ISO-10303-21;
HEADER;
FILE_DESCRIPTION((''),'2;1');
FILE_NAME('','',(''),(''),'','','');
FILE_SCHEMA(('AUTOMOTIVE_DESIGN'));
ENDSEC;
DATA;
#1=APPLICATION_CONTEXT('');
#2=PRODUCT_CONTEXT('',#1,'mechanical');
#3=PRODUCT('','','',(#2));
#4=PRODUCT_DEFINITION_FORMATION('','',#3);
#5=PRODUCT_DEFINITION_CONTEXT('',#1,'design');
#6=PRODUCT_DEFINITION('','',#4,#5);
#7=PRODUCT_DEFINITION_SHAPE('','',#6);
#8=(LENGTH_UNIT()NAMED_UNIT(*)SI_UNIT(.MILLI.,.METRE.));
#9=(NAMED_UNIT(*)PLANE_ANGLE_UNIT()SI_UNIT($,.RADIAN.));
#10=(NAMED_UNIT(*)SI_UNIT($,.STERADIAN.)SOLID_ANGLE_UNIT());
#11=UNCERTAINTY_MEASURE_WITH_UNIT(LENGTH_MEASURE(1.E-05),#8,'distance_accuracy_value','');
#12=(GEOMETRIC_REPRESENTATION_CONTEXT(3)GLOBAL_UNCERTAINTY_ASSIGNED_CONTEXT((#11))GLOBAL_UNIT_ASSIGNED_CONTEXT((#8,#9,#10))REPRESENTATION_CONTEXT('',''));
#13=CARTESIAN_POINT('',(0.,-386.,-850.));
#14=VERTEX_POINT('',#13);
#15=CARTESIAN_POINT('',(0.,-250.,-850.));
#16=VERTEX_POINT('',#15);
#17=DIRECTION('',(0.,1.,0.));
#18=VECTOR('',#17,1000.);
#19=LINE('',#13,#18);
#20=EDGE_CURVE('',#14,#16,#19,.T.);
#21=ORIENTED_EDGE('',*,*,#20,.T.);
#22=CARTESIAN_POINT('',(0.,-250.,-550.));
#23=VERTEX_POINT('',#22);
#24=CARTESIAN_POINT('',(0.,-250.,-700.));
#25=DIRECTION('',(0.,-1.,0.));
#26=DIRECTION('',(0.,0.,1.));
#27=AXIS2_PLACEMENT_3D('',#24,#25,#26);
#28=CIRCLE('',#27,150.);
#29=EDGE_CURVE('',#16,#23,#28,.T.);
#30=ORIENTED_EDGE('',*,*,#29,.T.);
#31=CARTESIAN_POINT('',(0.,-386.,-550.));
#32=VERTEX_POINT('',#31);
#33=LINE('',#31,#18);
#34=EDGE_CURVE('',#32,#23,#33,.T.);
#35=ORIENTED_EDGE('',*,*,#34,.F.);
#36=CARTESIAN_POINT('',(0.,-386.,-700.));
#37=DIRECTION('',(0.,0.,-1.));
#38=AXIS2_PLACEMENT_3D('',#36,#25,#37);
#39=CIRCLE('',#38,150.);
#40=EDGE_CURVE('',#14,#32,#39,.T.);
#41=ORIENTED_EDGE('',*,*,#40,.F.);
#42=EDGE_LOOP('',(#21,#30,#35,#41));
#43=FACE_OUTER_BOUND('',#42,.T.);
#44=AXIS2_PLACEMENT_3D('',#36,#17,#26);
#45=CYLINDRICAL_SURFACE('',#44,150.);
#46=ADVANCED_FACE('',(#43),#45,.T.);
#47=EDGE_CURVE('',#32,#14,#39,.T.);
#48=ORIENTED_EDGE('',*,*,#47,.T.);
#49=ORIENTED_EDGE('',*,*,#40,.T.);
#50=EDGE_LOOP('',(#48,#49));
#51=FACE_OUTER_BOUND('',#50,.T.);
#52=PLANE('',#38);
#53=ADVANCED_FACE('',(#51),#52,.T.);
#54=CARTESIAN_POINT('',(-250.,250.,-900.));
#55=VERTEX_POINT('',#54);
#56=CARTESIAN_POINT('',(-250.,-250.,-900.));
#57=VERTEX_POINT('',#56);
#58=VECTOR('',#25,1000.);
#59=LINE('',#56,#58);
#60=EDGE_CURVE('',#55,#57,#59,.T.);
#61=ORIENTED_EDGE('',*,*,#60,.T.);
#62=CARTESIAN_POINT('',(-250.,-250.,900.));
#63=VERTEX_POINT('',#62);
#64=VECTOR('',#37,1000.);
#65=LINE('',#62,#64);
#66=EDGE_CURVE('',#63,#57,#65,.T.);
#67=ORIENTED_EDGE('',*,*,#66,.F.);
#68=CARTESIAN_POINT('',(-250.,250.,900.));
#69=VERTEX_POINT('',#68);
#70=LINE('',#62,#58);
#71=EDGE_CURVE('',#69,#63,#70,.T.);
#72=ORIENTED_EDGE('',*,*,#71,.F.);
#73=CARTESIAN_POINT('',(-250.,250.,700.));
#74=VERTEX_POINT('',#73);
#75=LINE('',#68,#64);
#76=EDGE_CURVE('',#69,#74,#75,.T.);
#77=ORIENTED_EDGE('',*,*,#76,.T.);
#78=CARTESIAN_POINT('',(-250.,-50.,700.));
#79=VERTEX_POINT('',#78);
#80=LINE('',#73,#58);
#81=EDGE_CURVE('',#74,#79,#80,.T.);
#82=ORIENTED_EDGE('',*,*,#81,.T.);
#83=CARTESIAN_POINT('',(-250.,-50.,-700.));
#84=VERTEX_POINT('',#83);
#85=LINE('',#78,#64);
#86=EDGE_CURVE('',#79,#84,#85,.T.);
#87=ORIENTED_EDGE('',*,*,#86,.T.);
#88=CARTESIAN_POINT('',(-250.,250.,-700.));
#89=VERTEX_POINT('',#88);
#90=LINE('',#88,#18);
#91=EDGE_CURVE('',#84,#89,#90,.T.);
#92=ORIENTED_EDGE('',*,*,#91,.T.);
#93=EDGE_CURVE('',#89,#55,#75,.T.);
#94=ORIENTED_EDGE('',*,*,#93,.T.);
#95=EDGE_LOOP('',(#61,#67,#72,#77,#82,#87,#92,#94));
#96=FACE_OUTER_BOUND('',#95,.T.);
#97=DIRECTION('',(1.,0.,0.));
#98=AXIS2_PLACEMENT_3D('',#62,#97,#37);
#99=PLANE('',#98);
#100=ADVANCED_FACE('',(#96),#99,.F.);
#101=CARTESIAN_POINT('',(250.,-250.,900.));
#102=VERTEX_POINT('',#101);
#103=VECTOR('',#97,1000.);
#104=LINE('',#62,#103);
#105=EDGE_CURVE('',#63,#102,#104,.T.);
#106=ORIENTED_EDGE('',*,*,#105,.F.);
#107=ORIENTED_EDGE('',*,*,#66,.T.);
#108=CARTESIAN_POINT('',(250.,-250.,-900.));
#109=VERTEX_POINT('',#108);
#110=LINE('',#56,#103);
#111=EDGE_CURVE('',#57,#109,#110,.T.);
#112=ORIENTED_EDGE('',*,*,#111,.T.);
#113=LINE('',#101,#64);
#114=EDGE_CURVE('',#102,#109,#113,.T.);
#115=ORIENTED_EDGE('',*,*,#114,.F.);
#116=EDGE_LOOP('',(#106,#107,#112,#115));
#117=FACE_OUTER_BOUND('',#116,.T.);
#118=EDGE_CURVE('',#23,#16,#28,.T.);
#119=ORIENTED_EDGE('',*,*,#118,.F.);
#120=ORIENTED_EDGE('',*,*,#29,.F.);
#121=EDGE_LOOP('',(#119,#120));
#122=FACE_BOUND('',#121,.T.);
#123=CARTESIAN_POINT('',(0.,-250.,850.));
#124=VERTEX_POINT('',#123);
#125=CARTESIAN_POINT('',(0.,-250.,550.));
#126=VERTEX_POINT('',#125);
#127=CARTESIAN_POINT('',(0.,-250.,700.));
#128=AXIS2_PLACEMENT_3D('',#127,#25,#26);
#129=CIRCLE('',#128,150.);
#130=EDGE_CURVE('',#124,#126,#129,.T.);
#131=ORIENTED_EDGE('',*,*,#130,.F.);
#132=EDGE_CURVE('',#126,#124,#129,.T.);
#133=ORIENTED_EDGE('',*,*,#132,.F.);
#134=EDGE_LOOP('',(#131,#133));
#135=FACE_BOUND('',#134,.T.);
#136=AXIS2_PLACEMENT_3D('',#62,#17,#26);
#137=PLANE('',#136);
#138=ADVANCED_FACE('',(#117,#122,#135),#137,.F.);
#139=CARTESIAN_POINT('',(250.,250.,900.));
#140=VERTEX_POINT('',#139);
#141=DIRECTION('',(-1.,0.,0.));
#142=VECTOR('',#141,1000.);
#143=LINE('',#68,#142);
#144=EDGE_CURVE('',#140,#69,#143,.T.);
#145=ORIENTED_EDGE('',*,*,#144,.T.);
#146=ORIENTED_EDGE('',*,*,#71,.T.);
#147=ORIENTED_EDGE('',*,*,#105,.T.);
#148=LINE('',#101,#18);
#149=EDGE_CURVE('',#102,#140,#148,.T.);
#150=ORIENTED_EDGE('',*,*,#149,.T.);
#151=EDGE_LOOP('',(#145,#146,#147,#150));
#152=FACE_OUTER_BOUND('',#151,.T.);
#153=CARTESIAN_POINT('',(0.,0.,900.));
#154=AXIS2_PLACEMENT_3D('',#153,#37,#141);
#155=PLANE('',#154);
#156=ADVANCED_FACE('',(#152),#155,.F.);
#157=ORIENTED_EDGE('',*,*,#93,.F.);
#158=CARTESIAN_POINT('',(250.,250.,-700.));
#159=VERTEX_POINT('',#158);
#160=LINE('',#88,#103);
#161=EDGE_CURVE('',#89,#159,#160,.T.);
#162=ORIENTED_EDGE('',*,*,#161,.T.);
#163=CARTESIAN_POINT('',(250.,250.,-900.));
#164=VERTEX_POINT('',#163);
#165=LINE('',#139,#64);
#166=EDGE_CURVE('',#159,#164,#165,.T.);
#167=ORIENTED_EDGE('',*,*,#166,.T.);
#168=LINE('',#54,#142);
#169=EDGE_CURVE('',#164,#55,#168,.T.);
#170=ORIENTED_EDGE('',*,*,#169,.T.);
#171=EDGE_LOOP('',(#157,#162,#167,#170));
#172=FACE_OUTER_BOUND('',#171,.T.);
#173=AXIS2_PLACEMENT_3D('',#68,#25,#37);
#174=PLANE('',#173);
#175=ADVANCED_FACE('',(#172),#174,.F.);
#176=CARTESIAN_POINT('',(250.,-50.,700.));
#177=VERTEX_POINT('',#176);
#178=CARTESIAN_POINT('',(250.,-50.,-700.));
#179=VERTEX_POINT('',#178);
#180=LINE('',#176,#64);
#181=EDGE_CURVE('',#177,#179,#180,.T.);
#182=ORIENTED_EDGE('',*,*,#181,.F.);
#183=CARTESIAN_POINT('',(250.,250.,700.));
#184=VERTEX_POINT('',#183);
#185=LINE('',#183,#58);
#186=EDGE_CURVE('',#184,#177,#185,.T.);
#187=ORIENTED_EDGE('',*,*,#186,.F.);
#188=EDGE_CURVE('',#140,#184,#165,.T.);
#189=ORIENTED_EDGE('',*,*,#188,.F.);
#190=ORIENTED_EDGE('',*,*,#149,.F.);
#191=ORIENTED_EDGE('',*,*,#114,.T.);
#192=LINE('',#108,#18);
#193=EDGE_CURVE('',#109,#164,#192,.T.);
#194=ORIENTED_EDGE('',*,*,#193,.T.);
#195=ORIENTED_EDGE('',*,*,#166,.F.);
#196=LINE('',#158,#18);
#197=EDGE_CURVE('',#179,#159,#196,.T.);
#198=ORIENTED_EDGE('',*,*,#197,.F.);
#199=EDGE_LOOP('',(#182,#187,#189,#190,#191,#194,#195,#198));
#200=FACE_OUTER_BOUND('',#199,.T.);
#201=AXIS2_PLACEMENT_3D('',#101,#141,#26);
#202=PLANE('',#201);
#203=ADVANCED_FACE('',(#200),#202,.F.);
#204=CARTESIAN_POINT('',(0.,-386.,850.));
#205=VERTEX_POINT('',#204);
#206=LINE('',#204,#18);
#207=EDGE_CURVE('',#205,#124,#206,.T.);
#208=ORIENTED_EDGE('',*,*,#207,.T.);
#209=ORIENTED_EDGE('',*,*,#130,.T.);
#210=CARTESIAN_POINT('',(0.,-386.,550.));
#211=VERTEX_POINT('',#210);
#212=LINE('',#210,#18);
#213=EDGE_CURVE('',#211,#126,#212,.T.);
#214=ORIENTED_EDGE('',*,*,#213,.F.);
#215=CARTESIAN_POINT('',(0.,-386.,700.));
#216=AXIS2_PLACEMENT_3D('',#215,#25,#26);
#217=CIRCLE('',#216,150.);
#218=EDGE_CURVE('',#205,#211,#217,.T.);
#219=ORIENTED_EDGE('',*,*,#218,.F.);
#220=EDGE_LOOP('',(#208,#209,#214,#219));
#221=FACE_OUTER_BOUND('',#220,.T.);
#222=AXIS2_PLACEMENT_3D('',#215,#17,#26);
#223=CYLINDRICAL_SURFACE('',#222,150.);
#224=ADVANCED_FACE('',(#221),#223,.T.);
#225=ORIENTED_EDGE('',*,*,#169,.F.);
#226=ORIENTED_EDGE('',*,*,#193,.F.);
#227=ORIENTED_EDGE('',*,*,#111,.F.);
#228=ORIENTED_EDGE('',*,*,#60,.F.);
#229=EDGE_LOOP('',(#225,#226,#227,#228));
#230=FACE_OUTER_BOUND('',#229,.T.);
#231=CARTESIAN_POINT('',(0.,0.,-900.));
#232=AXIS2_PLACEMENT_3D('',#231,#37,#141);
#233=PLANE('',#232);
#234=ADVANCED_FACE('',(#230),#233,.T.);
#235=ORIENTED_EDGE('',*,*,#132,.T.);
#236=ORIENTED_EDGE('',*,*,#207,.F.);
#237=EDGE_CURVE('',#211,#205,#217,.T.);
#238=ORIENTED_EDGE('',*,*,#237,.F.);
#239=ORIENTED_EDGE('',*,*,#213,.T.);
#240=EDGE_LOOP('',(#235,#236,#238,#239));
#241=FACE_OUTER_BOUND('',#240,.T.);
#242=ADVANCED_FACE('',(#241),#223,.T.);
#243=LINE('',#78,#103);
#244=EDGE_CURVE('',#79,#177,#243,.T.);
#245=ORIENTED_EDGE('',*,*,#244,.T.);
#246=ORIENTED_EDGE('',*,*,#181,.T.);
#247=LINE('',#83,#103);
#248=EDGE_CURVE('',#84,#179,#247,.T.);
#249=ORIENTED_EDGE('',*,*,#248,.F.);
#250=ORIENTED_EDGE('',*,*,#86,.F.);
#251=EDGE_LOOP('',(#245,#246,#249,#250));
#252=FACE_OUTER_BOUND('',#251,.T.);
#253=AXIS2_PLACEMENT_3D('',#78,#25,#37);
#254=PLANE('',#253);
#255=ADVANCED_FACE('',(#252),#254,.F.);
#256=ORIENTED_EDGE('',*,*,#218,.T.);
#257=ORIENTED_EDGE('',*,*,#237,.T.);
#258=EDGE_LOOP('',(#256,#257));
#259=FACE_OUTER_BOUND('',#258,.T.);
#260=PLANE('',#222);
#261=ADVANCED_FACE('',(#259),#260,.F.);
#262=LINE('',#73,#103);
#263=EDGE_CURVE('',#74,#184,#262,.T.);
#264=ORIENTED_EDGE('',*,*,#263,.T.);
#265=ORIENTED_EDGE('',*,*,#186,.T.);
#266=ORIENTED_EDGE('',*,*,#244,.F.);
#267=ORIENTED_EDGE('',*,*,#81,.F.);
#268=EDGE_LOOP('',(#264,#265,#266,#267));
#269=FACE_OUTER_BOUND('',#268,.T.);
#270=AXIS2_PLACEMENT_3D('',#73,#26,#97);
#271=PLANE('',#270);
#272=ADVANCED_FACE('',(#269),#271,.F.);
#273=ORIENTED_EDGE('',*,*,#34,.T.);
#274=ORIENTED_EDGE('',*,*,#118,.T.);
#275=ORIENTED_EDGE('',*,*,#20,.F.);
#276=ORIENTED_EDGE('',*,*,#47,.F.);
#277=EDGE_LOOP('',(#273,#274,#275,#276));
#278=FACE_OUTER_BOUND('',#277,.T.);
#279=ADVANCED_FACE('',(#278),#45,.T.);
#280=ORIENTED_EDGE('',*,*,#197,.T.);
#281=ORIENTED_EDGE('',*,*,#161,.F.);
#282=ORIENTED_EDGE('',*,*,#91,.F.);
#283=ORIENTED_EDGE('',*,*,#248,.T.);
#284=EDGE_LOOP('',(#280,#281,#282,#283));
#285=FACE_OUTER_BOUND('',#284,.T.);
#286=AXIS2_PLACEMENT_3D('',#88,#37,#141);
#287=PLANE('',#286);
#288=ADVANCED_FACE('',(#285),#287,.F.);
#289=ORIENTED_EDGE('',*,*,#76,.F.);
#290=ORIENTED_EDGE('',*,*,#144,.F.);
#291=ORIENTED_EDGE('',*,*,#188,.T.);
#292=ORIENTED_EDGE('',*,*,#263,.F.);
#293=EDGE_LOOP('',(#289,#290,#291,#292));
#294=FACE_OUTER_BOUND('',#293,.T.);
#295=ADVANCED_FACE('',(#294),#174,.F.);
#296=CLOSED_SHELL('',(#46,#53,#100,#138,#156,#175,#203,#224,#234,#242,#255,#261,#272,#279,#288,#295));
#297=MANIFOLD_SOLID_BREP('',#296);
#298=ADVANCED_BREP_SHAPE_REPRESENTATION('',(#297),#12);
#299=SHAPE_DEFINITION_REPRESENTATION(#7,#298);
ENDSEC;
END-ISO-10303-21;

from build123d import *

# Parameters (mm, degrees)
SKETCH1_W           = 500
SKETCH1_H           = 500
BOSS_EXTRUDE1_DEPTH = 900
SKETCH2_R           = 150
BOSS_EXTRUDE2_DEPTH = 136
SKETCH3_W           = 1400
SKETCH3_H           = 300
CUT_EXTRUDE1_DEPTH  = 1100.543541657


with BuildPart() as part:
    # Sketch1 → Boss-Extrude1 (new, symmetric)
    with BuildSketch(Plane.XY):
        Rectangle(SKETCH1_W, SKETCH1_H)
    extrude(amount=BOSS_EXTRUDE1_DEPTH, both=True)

    # Sketch2 → Boss-Extrude2 (add)
    with BuildSketch(Plane.XZ.offset(250)):
        with Locations(Location((0, -700, 0), (0, 0, 90))):
            Circle(SKETCH2_R)
        with Locations(Location((0, 700, 0), (0, 0, 90))):
            Circle(SKETCH2_R)
    extrude(amount=BOSS_EXTRUDE2_DEPTH)

    # Sketch3 → Cut-Extrude1 (cut, through all)
    with BuildSketch(Plane(origin=(250, 0, 0), x_dir=(0, 0, -1), z_dir=(1, 0, 0))):
        with Locations((0, 100)):
            Rectangle(SKETCH3_W, SKETCH3_H)
    extrude(amount=-CUT_EXTRUDE1_DEPTH, mode=Mode.SUBTRACT)


solid = part.part
